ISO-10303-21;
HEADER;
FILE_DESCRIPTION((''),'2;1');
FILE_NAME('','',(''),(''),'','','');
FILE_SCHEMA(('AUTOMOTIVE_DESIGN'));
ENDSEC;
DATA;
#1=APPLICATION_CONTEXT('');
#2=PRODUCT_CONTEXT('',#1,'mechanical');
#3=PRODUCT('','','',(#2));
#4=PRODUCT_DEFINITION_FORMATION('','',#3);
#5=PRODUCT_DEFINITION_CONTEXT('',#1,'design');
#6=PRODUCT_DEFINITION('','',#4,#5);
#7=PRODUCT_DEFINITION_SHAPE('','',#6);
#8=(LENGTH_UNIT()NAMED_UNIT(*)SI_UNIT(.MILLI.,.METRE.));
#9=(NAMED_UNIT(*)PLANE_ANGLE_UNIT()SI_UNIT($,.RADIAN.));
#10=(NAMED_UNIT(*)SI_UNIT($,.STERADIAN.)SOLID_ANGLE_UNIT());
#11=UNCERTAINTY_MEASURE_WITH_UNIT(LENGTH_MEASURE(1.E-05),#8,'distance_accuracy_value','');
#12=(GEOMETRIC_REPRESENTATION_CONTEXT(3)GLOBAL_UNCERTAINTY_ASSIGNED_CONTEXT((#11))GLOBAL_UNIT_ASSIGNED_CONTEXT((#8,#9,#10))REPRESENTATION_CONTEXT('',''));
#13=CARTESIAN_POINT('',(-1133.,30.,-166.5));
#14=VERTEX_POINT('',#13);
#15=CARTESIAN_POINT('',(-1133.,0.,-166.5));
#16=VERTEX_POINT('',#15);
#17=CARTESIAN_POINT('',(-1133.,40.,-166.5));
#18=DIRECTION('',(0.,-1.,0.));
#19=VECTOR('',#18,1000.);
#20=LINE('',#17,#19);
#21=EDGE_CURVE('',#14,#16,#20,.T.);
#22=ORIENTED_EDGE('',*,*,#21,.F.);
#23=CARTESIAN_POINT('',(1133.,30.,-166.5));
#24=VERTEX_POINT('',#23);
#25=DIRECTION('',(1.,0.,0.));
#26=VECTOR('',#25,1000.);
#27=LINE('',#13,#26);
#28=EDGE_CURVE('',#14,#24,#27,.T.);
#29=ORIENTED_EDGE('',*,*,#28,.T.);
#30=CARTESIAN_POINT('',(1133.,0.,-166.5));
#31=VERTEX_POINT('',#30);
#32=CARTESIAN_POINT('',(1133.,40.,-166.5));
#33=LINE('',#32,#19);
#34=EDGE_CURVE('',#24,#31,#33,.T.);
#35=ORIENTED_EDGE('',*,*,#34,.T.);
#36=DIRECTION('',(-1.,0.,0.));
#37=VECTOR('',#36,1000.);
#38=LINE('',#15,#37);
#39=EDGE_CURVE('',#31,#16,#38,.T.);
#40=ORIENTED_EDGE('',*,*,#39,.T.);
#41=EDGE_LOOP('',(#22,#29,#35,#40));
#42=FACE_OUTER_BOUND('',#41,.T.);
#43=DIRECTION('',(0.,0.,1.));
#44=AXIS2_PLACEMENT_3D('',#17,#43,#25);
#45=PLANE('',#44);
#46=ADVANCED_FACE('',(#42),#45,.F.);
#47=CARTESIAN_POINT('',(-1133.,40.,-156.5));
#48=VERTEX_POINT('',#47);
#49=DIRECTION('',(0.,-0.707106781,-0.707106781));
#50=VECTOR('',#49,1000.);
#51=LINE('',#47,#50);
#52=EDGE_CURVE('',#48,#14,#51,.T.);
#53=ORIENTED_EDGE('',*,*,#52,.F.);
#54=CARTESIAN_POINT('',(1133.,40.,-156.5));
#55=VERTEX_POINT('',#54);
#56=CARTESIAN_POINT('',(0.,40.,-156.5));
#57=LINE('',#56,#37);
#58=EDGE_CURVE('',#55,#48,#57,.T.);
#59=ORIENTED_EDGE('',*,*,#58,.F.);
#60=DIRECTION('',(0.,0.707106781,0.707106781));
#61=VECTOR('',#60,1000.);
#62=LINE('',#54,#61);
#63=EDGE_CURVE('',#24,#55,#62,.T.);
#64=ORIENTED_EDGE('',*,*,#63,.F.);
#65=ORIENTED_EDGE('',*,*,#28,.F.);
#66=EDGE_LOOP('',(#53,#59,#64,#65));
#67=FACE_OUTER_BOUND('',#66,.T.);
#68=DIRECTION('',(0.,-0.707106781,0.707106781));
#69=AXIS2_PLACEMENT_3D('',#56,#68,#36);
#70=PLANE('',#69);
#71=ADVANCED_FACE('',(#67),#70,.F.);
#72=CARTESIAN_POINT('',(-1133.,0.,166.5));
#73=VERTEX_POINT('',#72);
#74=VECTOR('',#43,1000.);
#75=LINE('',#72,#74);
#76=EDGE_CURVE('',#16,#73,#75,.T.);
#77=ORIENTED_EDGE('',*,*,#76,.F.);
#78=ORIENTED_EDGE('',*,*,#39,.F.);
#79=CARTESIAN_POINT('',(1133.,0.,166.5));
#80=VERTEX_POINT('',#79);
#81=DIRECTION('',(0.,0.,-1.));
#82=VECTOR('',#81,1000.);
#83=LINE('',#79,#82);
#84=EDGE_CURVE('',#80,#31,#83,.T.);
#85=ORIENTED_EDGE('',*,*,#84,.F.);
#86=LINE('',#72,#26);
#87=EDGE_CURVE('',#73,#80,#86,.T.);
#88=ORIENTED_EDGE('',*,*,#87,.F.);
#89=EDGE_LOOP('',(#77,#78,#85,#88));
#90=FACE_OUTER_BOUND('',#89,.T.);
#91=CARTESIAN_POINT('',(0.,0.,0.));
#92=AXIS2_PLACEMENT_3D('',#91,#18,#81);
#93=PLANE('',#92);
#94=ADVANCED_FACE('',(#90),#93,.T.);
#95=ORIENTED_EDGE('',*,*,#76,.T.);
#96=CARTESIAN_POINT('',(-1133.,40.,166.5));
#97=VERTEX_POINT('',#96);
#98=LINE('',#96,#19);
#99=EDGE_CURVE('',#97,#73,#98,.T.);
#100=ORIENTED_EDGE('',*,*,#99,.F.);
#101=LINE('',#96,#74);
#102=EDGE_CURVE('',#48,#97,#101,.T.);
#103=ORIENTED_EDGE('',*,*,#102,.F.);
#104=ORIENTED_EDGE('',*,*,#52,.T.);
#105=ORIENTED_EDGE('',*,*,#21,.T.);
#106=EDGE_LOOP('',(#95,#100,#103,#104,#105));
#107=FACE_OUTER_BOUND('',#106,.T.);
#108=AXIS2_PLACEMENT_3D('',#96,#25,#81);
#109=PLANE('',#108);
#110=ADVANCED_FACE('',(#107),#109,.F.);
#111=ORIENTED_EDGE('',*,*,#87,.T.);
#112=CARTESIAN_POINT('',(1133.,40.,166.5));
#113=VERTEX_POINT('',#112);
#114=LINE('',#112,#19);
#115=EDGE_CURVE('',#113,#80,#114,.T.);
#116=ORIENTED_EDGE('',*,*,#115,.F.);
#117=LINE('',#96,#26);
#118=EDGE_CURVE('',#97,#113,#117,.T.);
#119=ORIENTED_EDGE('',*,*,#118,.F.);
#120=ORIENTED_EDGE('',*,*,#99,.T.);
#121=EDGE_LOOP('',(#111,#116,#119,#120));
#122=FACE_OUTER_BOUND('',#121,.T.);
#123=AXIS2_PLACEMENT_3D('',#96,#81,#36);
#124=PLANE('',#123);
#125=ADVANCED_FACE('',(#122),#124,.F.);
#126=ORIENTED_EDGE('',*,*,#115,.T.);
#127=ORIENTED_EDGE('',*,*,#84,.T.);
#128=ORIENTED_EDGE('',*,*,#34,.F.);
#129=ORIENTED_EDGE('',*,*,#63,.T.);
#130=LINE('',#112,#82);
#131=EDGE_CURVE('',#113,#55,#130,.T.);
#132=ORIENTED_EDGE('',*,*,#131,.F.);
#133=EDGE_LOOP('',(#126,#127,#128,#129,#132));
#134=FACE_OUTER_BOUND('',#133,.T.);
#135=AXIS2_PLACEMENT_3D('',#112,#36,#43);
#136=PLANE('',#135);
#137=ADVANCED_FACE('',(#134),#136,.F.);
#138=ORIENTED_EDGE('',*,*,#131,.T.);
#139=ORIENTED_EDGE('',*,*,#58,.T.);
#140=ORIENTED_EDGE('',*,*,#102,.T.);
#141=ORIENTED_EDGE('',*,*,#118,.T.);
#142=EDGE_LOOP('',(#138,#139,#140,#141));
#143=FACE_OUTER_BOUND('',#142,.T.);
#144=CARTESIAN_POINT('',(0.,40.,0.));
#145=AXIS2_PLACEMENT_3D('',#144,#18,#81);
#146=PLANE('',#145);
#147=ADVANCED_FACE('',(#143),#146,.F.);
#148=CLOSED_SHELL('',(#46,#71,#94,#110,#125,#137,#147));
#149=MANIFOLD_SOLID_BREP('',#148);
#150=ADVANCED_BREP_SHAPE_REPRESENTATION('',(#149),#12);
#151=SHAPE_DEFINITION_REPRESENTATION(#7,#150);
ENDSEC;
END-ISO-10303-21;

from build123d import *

# Parameters (mm, degrees)
SKETCH_1_W      = 2266
SKETCH_1_H      = 333
EXTRUDE_1_DEPTH = 40
CHAMFER_1_SIZE  = 10


with BuildPart() as part:
    # 草图1 → 凸台-拉伸1 (new body)
    with BuildSketch(Plane(origin=(0, 0, 0), x_dir=(1, 0, 0), z_dir=(0, 1, 0))):
        Rectangle(SKETCH_1_W, SKETCH_1_H)
    extrude(amount=EXTRUDE_1_DEPTH)

    # 倒角1
    chamfer_1_edges = [part.edges().sort_by_distance(p)[0] for p in [
        (0, 40, -166.5),
    ]]
    chamfer(chamfer_1_edges, length=CHAMFER_1_SIZE)


solid = part.part
